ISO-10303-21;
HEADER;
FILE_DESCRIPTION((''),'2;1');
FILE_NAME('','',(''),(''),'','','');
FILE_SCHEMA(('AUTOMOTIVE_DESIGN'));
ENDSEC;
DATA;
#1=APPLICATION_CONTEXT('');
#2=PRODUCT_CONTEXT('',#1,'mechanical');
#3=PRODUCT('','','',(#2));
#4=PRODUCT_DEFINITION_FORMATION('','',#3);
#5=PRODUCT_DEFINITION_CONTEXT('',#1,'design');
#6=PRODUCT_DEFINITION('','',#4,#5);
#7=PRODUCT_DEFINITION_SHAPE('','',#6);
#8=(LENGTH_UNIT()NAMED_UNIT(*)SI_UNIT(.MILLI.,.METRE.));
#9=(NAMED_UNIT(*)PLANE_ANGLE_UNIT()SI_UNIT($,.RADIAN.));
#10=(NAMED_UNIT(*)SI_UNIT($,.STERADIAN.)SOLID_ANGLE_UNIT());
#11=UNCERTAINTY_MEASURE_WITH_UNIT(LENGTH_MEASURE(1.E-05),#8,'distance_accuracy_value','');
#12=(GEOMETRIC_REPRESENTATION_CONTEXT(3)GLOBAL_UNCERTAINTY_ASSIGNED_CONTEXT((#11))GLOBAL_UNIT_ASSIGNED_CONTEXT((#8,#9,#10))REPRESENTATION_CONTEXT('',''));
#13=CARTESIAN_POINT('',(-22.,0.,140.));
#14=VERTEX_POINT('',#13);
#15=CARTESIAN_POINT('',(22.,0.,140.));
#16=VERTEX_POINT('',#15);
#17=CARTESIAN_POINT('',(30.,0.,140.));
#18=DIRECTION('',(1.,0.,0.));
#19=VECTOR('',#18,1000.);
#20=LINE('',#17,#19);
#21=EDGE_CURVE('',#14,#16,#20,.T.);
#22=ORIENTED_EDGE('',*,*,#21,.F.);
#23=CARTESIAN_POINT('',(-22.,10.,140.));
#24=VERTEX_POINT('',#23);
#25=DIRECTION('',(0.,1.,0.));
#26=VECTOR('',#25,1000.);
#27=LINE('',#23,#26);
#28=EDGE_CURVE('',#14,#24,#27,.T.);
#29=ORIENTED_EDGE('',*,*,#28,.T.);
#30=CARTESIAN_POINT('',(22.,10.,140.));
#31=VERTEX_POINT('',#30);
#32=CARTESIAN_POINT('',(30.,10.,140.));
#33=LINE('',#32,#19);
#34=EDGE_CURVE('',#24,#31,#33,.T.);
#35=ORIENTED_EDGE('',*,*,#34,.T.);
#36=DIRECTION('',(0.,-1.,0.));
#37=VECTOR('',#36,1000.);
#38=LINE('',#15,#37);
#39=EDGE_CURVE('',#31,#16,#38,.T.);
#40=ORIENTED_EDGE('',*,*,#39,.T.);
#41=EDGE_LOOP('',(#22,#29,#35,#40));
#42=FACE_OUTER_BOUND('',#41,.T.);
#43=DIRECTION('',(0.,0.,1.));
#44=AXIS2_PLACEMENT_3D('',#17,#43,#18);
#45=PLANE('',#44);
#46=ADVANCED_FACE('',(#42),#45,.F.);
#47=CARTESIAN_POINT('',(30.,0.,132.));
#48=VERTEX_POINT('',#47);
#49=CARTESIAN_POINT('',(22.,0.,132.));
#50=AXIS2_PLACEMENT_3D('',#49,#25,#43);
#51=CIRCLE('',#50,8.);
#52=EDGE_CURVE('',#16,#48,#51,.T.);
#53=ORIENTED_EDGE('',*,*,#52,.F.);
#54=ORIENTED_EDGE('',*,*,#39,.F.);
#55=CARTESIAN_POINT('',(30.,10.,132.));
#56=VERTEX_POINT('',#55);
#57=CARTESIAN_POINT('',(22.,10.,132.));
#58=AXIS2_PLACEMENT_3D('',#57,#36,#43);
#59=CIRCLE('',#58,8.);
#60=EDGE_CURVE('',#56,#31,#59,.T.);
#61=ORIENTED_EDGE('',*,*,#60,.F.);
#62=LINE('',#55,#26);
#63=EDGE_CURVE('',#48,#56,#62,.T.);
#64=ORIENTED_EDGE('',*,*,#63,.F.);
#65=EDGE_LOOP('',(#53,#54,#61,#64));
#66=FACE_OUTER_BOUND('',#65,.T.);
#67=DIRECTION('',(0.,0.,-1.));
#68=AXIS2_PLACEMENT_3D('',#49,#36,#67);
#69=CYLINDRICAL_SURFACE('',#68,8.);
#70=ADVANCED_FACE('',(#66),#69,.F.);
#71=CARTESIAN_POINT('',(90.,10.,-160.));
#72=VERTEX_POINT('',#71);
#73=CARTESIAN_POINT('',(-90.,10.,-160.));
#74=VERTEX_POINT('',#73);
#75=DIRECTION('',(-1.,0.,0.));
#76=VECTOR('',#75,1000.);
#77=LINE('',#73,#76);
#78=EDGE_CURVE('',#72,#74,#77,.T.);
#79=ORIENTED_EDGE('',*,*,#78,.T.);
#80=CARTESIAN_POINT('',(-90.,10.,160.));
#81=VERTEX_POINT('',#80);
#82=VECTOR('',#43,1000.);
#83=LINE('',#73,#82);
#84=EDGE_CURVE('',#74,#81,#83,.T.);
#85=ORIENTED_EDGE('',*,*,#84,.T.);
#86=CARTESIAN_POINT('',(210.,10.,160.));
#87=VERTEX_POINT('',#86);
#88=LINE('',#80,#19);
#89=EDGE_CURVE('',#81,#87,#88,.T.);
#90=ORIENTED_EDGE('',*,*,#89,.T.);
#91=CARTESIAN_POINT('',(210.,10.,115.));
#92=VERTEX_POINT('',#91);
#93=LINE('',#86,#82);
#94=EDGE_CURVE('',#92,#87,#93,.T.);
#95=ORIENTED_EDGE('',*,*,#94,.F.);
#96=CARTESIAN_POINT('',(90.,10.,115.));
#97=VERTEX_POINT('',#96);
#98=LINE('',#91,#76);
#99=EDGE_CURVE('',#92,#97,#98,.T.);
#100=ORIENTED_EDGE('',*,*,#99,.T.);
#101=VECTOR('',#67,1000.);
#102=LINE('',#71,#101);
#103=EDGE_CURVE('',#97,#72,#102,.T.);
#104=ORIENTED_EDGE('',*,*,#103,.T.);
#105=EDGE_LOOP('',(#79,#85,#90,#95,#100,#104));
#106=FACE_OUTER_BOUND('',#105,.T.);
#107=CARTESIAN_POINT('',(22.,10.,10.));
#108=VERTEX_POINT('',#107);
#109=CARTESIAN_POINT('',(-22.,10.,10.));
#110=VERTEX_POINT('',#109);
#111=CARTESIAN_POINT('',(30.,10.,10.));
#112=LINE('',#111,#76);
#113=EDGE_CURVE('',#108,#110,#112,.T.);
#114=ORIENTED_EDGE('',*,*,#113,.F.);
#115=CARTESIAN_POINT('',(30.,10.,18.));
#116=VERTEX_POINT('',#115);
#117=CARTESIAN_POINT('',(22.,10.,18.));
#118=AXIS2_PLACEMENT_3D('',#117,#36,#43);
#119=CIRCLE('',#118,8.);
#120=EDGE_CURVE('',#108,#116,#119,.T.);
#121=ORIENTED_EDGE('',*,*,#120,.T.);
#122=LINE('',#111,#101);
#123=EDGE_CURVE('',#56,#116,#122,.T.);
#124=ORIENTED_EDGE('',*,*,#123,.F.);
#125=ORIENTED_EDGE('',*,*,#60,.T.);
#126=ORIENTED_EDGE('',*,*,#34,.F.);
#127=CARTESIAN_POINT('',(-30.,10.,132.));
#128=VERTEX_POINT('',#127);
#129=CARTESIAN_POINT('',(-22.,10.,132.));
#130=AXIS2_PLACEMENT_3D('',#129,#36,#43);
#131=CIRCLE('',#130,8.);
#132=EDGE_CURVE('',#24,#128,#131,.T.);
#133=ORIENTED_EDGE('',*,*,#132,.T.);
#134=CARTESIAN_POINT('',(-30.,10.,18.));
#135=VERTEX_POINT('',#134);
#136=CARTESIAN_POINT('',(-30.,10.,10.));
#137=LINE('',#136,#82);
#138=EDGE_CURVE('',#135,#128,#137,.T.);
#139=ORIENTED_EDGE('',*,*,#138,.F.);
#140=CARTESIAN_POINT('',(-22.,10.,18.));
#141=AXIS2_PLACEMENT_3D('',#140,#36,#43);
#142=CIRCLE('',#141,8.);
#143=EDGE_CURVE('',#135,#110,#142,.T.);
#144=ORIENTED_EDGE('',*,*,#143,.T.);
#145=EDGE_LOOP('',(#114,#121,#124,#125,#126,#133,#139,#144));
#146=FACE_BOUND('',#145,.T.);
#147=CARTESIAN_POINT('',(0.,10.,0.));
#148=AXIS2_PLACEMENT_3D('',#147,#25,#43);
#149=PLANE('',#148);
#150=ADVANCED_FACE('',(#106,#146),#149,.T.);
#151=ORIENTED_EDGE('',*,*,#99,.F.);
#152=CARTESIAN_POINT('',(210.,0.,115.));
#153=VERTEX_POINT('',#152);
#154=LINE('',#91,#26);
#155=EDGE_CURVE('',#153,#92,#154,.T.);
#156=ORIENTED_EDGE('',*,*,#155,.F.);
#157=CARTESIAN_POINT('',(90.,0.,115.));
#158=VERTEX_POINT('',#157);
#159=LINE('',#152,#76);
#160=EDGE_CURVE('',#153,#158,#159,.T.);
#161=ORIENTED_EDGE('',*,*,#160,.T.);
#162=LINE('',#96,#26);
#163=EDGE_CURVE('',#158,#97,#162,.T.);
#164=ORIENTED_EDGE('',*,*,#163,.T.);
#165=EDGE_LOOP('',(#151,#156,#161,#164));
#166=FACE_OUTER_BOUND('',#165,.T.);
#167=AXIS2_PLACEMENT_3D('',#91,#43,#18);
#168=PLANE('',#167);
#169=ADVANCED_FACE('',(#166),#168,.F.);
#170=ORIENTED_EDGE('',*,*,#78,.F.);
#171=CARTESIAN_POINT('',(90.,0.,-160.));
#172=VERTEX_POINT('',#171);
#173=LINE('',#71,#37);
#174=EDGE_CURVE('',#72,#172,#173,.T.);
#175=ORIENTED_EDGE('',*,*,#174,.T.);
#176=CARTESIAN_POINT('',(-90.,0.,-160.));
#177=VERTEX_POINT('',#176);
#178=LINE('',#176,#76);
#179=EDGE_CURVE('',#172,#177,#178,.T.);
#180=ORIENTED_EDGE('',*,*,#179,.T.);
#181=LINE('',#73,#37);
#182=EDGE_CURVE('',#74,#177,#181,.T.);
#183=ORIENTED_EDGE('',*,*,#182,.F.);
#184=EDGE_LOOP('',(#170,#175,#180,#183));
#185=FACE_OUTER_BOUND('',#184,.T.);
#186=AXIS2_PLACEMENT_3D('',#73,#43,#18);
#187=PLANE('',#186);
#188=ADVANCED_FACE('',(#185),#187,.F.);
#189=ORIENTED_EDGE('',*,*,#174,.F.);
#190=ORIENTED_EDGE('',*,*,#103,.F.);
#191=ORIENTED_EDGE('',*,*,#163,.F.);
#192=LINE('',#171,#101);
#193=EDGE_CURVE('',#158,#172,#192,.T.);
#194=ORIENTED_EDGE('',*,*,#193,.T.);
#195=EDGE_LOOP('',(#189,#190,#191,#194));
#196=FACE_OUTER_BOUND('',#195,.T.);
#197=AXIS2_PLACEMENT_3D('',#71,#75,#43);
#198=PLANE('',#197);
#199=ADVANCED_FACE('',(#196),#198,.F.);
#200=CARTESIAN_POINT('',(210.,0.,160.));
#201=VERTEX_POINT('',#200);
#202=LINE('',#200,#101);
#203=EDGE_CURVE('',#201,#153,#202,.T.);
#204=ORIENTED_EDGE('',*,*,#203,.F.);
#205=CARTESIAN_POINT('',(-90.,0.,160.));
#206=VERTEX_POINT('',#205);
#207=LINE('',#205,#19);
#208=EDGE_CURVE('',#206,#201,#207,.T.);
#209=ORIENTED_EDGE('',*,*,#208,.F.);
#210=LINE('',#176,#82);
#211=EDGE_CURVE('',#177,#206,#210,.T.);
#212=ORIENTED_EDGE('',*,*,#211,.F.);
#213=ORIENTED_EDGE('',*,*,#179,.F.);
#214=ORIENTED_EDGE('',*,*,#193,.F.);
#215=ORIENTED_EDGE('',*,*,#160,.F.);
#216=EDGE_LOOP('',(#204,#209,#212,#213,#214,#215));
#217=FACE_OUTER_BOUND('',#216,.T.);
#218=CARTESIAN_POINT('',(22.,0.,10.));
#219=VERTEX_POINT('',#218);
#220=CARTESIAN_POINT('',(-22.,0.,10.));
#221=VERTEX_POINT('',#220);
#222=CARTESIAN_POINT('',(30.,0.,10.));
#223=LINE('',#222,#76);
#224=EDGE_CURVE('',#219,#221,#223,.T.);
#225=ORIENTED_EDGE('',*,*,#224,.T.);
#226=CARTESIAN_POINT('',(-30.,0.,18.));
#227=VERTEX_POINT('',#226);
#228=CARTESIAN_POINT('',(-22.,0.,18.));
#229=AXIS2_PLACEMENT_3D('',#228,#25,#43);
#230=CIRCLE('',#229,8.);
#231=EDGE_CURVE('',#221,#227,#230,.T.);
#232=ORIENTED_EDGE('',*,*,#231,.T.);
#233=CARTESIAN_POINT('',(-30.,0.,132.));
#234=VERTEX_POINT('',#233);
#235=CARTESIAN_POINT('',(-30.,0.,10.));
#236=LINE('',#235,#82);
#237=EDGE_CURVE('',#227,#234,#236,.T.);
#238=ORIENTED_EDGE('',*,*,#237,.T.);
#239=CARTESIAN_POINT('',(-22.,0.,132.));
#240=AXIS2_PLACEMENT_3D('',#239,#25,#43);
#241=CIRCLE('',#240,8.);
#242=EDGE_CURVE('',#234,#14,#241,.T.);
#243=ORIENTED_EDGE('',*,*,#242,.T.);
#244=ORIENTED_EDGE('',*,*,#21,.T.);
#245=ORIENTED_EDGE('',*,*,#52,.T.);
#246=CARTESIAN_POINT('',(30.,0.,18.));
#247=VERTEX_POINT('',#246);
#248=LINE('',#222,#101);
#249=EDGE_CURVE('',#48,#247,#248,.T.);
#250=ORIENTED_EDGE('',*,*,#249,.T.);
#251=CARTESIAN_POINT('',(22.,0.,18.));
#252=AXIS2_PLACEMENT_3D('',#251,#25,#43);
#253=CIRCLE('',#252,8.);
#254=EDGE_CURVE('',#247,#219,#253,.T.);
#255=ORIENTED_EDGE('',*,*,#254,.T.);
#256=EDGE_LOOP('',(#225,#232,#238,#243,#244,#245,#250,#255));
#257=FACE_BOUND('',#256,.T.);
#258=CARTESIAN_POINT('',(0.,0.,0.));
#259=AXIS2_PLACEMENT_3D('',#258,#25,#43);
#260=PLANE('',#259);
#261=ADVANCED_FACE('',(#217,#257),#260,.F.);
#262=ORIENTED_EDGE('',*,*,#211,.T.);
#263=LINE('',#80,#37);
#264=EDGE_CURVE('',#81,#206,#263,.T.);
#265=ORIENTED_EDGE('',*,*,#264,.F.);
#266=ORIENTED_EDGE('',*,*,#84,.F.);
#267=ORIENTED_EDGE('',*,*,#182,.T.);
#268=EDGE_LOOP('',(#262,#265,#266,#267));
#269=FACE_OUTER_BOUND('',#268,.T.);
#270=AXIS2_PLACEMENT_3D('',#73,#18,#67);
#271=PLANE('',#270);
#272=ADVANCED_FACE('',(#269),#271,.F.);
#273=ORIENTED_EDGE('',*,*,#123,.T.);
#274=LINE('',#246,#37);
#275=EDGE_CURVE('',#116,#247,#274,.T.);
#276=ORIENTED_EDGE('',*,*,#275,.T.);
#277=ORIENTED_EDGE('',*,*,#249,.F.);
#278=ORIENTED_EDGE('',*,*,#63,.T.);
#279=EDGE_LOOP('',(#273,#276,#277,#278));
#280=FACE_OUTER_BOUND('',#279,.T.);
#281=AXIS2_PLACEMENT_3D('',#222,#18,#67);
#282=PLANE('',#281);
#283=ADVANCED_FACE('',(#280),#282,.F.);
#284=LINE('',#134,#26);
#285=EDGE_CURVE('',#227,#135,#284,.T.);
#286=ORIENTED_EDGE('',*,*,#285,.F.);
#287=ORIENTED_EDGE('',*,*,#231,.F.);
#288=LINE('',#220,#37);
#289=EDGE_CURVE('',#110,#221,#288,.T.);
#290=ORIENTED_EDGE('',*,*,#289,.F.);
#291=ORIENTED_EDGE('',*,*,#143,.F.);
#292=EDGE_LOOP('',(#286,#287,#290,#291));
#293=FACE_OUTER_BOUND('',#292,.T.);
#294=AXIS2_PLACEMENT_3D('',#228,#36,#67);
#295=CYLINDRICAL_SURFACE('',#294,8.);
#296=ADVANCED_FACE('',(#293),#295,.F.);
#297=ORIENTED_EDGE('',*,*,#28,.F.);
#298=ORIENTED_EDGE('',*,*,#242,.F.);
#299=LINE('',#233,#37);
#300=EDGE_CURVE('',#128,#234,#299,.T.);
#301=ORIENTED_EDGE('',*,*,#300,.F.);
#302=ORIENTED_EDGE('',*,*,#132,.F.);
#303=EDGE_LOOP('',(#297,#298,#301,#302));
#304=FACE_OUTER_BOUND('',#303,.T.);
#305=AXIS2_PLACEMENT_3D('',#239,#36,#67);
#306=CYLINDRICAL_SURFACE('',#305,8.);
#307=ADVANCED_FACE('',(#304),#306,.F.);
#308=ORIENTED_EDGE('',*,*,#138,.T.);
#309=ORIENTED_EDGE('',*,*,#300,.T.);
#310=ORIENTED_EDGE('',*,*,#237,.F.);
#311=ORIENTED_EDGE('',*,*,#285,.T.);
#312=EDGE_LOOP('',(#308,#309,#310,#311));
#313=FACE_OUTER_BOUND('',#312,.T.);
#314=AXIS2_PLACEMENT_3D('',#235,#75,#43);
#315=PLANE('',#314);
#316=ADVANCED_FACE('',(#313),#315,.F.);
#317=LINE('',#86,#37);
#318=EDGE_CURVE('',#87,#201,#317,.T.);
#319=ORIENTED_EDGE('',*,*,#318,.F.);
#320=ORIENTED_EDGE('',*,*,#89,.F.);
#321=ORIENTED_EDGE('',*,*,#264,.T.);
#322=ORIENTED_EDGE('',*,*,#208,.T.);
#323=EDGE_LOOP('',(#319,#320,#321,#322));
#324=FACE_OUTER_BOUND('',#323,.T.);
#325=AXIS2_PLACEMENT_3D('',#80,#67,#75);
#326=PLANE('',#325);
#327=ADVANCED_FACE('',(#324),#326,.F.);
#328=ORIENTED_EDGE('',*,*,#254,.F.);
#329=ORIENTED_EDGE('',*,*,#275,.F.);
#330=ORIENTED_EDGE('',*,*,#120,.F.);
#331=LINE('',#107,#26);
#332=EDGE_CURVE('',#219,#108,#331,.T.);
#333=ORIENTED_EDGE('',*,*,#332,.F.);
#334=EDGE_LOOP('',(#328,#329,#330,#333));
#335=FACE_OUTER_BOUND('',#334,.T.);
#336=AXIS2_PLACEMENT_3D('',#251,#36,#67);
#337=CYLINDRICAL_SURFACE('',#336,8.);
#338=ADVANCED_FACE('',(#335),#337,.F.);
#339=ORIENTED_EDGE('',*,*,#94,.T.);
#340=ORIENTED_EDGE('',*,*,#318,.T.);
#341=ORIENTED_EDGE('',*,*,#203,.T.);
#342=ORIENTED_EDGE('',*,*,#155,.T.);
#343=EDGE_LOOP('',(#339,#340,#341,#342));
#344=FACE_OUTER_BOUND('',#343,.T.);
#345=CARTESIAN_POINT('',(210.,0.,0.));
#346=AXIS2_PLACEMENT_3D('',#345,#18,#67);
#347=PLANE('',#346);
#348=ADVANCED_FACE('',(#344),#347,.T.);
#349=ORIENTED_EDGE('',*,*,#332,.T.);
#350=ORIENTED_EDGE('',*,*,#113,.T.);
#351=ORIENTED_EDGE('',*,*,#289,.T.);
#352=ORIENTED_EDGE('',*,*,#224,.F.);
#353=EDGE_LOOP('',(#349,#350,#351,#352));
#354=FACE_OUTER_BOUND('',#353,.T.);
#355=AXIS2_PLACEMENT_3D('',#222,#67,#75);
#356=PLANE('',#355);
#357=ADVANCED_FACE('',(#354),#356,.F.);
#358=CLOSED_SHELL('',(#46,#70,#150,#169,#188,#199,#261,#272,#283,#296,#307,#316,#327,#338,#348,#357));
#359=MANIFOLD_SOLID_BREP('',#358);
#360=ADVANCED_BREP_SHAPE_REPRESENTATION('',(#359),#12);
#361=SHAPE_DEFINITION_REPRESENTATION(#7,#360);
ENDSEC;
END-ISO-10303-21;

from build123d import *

# Parameters (mm, degrees)
SKETCH1_W           = 180
SKETCH1_H           = 320
BOSS_EXTRUDE1_DEPTH = 10
SKETCH2_W           = 60
SKETCH2_H           = 130
CUT_EXTRUDE1_DEPTH  = 184.847763109
FILLET1_R           = 8
SKETCH3_W           = 45
SKETCH3_H           = 10
BOSS_EXTRUDE2_DEPTH = 120


with BuildPart() as part:
    # Sketch1 → Boss-Extrude1 (new body)
    with BuildSketch(Plane(origin=(0, 0, 0), x_dir=(1, 0, 0), z_dir=(0, 1, 0))):
        Rectangle(SKETCH1_W, SKETCH1_H)
    extrude(amount=BOSS_EXTRUDE1_DEPTH)

    # Sketch2 → Cut-Extrude1 (cut, through all)
    with BuildSketch(Plane(origin=(0, 10, 0), x_dir=(1, 0, 0), z_dir=(0, 1, 0))):
        with Locations((0, -75)):
            Rectangle(SKETCH2_W, SKETCH2_H)
    extrude(amount=-CUT_EXTRUDE1_DEPTH, mode=Mode.SUBTRACT)

    # Fillet1
    fillet1_edges = [part.edges().sort_by_distance(p)[0] for p in [
        (30, 5, 10),
        (30, 5, 140),
        (-30, 5, 140),
        (-30, 5, 10),
    ]]
    fillet(fillet1_edges, radius=FILLET1_R)

    # Sketch3 → Boss-Extrude2 (add)
    with BuildSketch(Plane(origin=(90, 0, 0), x_dir=(0, 0, -1), z_dir=(1, 0, 0))):
        with Locations((-137.5, 5)):
            Rectangle(SKETCH3_W, SKETCH3_H)
    extrude(amount=BOSS_EXTRUDE2_DEPTH)


solid = part.part
